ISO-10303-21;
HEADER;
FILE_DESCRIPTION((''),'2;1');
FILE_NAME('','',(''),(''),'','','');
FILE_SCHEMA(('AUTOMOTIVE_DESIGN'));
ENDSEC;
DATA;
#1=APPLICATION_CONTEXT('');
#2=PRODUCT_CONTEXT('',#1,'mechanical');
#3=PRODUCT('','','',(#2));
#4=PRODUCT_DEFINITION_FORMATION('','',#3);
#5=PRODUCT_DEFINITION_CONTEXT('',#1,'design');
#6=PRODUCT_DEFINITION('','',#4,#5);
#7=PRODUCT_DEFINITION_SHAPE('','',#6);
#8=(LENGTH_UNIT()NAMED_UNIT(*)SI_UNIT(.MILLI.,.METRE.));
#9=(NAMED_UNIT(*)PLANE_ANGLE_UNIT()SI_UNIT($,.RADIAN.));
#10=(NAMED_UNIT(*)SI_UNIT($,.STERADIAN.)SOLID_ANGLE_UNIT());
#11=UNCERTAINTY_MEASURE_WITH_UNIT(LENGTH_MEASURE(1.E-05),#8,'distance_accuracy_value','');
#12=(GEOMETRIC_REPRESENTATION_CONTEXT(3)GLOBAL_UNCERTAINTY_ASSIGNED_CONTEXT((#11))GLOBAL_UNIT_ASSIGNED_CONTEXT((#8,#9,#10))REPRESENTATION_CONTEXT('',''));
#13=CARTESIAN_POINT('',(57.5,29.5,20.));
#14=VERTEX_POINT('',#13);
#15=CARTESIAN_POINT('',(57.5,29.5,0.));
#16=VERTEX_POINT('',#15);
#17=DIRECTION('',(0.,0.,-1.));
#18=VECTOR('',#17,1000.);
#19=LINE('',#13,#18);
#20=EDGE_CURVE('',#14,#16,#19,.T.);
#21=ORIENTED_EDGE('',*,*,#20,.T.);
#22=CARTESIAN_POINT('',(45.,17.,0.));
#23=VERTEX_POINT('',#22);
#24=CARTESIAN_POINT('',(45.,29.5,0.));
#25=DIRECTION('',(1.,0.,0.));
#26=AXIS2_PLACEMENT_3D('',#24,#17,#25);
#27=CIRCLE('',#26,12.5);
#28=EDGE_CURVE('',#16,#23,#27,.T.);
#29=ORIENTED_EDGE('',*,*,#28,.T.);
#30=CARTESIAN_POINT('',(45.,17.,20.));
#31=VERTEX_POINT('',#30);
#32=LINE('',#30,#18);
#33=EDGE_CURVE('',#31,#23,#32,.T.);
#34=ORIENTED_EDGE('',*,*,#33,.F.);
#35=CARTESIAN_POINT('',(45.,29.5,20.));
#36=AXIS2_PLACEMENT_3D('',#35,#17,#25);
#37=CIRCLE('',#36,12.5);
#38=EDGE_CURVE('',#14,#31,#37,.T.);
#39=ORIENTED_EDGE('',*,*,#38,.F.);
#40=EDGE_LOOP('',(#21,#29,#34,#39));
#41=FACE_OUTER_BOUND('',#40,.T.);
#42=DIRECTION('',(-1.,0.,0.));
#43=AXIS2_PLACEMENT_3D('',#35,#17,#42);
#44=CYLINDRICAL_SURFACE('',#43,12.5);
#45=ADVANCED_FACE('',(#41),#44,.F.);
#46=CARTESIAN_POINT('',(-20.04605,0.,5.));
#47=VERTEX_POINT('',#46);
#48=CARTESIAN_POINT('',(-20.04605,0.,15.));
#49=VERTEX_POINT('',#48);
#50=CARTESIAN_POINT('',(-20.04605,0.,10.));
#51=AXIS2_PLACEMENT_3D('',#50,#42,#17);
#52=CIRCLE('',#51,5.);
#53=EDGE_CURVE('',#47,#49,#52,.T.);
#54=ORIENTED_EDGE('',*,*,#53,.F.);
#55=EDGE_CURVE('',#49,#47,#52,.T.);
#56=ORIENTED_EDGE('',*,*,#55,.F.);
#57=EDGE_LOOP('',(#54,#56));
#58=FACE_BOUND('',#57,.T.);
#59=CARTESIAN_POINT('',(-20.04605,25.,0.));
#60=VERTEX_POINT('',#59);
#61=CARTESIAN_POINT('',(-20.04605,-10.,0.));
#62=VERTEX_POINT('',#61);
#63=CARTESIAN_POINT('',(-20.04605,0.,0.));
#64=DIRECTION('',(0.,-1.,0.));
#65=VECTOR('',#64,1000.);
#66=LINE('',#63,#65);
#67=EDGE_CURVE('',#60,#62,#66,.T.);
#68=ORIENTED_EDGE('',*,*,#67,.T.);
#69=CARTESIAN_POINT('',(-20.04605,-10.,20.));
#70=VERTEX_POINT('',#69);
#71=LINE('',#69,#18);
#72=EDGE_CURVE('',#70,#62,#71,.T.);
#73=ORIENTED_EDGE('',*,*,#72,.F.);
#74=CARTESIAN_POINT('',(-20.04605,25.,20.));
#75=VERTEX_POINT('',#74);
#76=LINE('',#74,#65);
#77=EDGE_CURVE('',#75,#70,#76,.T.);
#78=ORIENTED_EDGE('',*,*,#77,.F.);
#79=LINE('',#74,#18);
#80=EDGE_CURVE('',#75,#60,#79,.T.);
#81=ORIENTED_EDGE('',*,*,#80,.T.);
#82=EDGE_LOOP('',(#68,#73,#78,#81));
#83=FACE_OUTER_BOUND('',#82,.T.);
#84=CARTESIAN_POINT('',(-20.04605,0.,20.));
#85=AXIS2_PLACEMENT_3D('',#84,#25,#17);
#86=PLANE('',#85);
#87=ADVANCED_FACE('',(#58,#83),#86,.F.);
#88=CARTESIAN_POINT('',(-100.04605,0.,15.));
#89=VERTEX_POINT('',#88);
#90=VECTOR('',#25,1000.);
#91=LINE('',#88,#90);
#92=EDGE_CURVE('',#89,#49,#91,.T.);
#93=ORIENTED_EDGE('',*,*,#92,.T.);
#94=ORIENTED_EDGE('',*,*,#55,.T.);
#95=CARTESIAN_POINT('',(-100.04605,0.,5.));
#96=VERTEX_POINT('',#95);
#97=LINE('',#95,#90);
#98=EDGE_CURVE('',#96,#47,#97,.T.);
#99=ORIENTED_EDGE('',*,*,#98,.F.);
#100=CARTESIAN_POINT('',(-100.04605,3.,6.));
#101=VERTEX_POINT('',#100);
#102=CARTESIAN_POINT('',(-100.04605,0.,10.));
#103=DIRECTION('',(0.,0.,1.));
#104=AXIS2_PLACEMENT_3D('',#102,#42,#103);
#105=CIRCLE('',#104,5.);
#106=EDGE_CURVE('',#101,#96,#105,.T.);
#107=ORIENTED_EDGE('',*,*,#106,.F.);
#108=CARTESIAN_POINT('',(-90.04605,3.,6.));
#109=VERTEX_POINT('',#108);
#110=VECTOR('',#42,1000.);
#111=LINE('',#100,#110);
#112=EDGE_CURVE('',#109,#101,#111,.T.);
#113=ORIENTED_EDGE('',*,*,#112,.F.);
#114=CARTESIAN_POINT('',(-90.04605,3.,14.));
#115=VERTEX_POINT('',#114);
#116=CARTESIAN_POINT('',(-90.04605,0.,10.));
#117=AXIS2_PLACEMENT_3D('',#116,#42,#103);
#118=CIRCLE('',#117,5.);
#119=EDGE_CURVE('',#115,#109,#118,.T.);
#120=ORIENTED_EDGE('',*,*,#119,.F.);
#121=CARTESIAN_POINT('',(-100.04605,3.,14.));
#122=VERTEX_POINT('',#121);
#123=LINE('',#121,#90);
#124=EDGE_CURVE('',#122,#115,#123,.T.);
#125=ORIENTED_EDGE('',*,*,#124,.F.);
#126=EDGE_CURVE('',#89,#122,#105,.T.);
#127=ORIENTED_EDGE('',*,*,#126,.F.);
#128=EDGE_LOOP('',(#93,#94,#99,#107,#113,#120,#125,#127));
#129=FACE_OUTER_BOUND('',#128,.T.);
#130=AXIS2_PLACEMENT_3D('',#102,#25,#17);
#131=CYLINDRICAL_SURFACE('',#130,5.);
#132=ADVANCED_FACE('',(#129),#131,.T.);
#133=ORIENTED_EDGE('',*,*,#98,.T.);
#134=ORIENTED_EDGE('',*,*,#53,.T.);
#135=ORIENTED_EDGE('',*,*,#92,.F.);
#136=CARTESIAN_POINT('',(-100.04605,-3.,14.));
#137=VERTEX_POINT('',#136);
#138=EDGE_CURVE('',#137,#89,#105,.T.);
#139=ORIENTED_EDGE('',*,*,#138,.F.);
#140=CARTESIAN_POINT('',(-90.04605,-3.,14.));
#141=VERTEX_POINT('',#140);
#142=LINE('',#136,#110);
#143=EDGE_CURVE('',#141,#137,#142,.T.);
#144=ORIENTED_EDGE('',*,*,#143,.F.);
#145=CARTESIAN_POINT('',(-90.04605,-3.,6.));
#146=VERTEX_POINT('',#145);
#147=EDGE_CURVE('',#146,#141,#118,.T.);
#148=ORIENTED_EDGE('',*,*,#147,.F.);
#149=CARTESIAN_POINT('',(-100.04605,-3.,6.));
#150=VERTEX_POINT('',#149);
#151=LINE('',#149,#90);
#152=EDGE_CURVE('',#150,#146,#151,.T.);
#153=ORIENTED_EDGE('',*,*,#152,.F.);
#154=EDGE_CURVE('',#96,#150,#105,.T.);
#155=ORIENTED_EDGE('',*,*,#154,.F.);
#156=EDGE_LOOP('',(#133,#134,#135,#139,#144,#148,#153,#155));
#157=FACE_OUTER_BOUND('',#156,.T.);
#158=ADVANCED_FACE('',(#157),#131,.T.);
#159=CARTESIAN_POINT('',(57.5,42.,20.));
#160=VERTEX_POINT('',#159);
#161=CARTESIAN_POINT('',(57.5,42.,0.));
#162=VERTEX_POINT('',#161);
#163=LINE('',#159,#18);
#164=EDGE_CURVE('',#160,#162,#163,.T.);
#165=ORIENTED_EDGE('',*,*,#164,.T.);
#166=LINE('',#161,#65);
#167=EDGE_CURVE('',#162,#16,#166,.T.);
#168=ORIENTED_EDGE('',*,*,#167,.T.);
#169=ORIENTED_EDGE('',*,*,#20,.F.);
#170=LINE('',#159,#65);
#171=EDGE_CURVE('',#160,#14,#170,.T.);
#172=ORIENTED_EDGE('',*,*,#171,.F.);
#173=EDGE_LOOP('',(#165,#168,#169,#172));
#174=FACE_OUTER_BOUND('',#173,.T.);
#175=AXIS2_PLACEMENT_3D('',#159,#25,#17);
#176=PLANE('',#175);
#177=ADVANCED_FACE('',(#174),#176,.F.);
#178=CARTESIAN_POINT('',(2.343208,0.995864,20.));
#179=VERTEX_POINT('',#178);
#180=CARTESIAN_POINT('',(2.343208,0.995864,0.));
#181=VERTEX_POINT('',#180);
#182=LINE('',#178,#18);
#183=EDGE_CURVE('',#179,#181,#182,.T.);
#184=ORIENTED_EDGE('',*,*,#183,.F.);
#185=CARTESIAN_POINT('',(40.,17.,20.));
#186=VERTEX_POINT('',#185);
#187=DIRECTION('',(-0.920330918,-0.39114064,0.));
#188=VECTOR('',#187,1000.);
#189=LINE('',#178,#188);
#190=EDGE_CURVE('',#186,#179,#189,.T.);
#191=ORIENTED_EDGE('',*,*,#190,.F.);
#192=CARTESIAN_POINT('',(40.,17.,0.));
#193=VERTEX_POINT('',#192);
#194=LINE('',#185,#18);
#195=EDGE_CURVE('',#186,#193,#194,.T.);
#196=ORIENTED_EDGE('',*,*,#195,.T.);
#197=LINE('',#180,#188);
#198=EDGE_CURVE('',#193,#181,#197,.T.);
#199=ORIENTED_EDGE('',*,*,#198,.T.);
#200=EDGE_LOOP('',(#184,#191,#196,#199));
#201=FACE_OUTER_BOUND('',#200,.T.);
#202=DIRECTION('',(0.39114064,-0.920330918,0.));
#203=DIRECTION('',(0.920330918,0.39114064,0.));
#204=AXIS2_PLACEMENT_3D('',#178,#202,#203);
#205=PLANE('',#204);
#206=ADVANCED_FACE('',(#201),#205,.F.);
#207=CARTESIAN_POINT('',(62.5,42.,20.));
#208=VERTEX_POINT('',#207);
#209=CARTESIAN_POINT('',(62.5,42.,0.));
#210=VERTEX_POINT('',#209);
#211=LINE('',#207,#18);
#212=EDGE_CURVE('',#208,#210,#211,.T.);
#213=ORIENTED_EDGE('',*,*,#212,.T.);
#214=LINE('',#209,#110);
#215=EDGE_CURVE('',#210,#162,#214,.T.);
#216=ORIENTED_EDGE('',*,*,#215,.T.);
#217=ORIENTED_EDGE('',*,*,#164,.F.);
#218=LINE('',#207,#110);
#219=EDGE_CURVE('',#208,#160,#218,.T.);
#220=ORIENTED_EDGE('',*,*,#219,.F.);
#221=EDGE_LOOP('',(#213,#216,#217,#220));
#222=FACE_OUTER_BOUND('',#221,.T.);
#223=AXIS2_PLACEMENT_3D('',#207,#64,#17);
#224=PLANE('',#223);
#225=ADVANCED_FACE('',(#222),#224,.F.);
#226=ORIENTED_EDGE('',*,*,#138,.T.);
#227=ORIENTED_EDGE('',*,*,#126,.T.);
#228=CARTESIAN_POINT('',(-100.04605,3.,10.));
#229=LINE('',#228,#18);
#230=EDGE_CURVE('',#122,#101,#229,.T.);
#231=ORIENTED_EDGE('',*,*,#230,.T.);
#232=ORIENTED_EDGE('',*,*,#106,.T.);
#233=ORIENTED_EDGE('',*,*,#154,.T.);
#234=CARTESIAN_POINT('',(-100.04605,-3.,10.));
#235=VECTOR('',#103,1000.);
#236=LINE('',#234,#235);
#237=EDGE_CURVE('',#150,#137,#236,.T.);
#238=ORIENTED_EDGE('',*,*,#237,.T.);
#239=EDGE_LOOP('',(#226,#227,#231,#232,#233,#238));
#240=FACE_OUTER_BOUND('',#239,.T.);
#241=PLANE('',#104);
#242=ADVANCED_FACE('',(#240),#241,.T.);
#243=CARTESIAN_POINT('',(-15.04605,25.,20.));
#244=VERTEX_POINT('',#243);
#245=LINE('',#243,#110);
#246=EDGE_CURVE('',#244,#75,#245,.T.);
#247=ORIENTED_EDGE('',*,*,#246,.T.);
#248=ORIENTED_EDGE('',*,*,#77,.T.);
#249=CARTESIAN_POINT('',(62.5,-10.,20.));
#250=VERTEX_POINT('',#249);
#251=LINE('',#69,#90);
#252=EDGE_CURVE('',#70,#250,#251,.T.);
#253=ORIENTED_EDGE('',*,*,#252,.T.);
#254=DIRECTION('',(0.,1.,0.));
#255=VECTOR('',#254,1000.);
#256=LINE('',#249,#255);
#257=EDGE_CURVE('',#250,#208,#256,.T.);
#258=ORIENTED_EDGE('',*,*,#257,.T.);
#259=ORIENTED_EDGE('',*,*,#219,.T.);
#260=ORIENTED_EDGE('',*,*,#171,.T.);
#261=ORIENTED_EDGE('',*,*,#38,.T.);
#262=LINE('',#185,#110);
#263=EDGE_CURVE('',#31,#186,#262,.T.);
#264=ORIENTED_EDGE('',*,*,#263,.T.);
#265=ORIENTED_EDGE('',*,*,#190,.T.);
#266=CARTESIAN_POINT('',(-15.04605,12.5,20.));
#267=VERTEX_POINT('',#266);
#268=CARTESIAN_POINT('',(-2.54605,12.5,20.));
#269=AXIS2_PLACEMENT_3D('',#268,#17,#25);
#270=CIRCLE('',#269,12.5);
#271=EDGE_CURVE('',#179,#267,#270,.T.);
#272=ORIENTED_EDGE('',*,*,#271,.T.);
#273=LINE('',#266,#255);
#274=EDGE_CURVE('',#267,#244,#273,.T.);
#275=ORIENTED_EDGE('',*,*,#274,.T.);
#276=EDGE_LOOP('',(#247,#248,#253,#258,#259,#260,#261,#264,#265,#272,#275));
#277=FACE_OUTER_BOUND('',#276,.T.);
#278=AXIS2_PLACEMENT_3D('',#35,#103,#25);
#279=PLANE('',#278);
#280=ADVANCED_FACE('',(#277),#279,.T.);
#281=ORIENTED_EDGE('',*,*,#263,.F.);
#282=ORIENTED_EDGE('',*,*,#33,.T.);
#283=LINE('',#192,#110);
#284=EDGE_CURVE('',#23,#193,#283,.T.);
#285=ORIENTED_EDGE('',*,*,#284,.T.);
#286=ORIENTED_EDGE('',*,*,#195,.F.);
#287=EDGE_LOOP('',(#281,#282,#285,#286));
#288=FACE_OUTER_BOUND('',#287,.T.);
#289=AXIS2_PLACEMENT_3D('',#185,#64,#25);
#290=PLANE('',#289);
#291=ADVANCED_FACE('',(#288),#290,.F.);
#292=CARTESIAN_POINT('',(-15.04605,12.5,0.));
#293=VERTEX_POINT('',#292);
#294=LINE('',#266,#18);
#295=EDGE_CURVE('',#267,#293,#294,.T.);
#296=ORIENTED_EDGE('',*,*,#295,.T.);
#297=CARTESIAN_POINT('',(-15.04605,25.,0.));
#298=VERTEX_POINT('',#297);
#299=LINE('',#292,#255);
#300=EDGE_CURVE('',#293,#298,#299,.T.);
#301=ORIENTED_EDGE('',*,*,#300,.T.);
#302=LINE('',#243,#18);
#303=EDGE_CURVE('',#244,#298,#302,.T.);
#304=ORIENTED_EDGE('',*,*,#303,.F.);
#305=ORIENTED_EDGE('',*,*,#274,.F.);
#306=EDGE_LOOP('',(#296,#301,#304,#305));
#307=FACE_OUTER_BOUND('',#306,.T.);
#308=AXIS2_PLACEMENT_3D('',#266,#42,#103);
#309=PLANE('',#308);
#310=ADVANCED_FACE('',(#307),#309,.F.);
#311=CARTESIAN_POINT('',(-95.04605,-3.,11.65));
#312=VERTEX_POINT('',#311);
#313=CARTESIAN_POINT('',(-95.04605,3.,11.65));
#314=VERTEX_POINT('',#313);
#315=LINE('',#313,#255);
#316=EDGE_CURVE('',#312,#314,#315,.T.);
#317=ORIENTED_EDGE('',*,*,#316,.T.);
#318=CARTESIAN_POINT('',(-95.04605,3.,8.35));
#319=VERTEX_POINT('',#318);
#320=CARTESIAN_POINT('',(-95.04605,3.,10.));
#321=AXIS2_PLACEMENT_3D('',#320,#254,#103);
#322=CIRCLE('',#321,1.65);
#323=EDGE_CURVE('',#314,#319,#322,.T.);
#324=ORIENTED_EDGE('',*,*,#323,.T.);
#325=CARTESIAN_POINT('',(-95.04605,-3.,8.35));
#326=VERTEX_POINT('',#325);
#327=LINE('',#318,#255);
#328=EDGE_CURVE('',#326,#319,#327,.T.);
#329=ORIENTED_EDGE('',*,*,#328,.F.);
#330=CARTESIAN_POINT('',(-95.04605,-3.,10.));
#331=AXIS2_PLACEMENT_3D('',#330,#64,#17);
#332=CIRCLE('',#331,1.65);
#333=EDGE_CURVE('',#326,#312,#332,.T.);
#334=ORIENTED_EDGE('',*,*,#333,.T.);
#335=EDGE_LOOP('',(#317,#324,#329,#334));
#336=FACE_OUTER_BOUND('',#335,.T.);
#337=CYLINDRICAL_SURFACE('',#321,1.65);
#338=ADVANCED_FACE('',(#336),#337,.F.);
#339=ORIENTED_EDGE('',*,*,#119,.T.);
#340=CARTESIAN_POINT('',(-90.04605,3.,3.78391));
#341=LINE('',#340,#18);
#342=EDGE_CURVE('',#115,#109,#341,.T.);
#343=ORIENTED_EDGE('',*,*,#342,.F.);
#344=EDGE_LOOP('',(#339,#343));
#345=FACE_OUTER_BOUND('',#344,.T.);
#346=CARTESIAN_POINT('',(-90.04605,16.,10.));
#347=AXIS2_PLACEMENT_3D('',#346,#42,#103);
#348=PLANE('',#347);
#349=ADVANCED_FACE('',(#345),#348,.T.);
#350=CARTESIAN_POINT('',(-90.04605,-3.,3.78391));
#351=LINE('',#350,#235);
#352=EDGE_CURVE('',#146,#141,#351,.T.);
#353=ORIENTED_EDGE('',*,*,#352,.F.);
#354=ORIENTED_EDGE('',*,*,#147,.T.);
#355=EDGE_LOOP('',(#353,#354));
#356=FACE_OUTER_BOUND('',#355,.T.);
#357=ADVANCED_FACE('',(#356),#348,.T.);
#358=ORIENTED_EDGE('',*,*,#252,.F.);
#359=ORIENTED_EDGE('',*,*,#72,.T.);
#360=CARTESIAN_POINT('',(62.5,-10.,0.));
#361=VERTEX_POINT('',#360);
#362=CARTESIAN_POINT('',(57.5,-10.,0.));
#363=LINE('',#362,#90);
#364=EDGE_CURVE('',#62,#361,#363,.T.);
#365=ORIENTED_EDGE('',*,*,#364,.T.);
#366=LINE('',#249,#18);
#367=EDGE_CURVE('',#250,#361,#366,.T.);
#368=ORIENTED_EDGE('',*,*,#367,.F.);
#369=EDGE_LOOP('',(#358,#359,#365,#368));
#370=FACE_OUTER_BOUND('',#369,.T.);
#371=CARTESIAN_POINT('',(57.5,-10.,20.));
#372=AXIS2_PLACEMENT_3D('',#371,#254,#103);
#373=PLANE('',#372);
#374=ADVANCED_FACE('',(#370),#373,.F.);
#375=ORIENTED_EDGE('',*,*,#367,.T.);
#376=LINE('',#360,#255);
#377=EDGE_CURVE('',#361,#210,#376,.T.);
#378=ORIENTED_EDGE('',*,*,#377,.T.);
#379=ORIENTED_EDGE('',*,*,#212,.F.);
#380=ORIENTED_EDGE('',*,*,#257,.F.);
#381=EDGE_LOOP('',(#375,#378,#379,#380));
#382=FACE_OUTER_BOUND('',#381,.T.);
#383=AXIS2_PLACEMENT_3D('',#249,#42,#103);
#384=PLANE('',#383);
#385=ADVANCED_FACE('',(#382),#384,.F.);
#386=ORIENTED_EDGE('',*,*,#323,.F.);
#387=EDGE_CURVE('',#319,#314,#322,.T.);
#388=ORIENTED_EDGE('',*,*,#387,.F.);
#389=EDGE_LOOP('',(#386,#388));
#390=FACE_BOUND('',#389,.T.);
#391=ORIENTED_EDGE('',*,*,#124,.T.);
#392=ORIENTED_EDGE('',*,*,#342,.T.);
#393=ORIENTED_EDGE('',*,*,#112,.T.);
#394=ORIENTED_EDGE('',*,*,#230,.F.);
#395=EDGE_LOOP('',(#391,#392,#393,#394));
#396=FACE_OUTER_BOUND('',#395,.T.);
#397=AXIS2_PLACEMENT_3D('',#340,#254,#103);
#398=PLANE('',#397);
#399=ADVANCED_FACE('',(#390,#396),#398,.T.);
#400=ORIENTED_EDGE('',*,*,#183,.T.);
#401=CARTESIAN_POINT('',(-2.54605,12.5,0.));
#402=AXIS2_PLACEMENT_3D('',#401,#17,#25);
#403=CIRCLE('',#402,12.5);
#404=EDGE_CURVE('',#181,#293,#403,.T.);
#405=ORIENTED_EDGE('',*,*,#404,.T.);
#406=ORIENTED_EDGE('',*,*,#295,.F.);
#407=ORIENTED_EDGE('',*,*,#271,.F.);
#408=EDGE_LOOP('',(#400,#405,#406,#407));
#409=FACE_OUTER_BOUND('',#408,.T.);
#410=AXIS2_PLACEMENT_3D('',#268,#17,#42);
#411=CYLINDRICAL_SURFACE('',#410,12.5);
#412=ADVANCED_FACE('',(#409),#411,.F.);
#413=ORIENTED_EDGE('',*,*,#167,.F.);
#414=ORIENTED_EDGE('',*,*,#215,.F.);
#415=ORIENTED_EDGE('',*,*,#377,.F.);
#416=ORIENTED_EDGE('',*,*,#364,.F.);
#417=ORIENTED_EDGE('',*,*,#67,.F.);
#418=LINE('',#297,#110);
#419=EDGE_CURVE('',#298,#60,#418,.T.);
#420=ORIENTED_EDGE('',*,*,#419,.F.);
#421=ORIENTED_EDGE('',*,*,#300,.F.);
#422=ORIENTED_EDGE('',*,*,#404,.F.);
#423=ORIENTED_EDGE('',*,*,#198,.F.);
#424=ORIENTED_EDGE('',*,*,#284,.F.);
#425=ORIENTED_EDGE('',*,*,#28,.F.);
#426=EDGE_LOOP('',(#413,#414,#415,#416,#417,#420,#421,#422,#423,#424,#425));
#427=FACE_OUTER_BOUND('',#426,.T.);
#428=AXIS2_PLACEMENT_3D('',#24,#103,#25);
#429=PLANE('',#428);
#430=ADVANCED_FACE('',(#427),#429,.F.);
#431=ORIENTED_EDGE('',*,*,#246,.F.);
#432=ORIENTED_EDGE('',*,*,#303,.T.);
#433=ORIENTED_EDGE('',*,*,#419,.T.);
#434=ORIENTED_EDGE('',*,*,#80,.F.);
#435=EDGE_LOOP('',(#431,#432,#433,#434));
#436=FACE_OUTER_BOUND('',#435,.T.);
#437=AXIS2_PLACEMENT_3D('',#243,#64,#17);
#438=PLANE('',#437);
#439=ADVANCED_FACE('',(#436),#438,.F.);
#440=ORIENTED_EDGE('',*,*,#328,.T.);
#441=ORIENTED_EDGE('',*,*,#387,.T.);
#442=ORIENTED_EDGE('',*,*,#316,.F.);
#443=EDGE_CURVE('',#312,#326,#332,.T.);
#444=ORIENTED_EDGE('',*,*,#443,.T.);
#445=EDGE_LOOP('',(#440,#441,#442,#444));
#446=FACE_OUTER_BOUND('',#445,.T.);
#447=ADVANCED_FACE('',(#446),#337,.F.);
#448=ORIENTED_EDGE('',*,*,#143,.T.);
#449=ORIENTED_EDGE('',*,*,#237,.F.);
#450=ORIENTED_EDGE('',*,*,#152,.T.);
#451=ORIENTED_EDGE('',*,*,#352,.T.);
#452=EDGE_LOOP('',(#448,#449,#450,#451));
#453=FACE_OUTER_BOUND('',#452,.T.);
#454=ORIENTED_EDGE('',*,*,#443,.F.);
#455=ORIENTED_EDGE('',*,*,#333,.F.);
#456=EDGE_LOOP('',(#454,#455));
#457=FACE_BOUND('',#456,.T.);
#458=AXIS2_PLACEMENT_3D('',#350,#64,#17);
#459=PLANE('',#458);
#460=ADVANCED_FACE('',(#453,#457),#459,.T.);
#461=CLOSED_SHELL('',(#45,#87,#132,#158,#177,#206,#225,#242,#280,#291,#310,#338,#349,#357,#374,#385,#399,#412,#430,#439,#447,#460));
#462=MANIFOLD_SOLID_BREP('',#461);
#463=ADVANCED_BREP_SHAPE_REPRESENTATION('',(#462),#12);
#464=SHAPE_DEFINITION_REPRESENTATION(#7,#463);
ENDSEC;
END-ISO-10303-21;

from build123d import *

# Parameters (mm, degrees)
EXTRUDE_1_DEPTH        = 20
SKETCH_3_R             = 5
EXTRUDE_2_DEPTH        = 80
SKETCH_4_OUTSIDE_W     = 56.366
SKETCH_4_OUTSIDE_H     = 88.366
SKETCH_4_OUTSIDE_W_2   = 11.216089963
SKETCH_4_OUTSIDE_H_2   = 6
CUT_EXTRUDE_1_DEPTH    = 10
HOLE_WIZARD_M4_1_D     = 3.3
HOLE_WIZARD_M4_1_DEPTH = 10.1
HOLE_WIZARD_M4_1_TIP   = 0.991420021


with BuildPart() as part:
    # 草图2 → 凸台-拉伸1 (new body)
    with BuildSketch(Plane.XY):
        with BuildLine():
            Line((2.343208281, 0.995863519), (40, 17))
            Line((40, 17), (45, 17))
            ThreePointArc((45, 17), (53.838834765, 20.661165235), (57.5, 29.5))
            Line((57.5, 29.5), (57.5, 42))
            Line((57.5, 42), (62.5, 42))
            Line((62.5, 42), (62.5, -10))
            Line((62.5, -10), (57.5, -10))
            Line((57.5, -10), (40, -10))
            Line((40, -10), (-20.046049724, -10))
            Line((-20.046049724, -10), (-20.046049724, 0))
            Line((-20.046049724, 0), (-20.046049724, 25))
            Line((-20.046049724, 25), (-15.046049724, 25))
            Line((-15.046049724, 25), (-15.046049724, 12.5))
            ThreePointArc((-15.046049724, 12.5), (-9.442943044, 2.074892685), (2.343208281, 0.995863519))
        make_face()
    extrude(amount=EXTRUDE_1_DEPTH)

    # 草图3 → 凸台-拉伸2 (add)
    with BuildSketch(Plane.ZY.offset(20.046049724)):
        with Locations(Location((10, 0, 0), (0, 0, 180))):
            Circle(SKETCH_3_R)
    extrude(amount=EXTRUDE_2_DEPTH)

    # 草图4 outside → 切除-拉伸1 (cut)
    with BuildSketch(Plane.ZY.offset(100.046049724)):
        with Locations((10, 16)):
            Rectangle(SKETCH_4_OUTSIDE_W, SKETCH_4_OUTSIDE_H)
        with Locations((9.391955019, 0)):
            Rectangle(SKETCH_4_OUTSIDE_W_2, SKETCH_4_OUTSIDE_H_2, mode=Mode.SUBTRACT)
    extrude(amount=-CUT_EXTRUDE_1_DEPTH, mode=Mode.SUBTRACT)

    # M4 螺纹孔1
    with Locations(Plane(origin=(0, 3, 0), x_dir=(1, 0, 0), z_dir=(0, 1, 0))):
        with Locations((-95.046049724, -10)):
            Hole(HOLE_WIZARD_M4_1_D / 2, depth=HOLE_WIZARD_M4_1_DEPTH)
            with Locations((0, 0, -(HOLE_WIZARD_M4_1_DEPTH + HOLE_WIZARD_M4_1_TIP / 2))):  # 118° drill point
                Cone(0, HOLE_WIZARD_M4_1_D / 2, HOLE_WIZARD_M4_1_TIP, mode=Mode.SUBTRACT)


solid = part.part
